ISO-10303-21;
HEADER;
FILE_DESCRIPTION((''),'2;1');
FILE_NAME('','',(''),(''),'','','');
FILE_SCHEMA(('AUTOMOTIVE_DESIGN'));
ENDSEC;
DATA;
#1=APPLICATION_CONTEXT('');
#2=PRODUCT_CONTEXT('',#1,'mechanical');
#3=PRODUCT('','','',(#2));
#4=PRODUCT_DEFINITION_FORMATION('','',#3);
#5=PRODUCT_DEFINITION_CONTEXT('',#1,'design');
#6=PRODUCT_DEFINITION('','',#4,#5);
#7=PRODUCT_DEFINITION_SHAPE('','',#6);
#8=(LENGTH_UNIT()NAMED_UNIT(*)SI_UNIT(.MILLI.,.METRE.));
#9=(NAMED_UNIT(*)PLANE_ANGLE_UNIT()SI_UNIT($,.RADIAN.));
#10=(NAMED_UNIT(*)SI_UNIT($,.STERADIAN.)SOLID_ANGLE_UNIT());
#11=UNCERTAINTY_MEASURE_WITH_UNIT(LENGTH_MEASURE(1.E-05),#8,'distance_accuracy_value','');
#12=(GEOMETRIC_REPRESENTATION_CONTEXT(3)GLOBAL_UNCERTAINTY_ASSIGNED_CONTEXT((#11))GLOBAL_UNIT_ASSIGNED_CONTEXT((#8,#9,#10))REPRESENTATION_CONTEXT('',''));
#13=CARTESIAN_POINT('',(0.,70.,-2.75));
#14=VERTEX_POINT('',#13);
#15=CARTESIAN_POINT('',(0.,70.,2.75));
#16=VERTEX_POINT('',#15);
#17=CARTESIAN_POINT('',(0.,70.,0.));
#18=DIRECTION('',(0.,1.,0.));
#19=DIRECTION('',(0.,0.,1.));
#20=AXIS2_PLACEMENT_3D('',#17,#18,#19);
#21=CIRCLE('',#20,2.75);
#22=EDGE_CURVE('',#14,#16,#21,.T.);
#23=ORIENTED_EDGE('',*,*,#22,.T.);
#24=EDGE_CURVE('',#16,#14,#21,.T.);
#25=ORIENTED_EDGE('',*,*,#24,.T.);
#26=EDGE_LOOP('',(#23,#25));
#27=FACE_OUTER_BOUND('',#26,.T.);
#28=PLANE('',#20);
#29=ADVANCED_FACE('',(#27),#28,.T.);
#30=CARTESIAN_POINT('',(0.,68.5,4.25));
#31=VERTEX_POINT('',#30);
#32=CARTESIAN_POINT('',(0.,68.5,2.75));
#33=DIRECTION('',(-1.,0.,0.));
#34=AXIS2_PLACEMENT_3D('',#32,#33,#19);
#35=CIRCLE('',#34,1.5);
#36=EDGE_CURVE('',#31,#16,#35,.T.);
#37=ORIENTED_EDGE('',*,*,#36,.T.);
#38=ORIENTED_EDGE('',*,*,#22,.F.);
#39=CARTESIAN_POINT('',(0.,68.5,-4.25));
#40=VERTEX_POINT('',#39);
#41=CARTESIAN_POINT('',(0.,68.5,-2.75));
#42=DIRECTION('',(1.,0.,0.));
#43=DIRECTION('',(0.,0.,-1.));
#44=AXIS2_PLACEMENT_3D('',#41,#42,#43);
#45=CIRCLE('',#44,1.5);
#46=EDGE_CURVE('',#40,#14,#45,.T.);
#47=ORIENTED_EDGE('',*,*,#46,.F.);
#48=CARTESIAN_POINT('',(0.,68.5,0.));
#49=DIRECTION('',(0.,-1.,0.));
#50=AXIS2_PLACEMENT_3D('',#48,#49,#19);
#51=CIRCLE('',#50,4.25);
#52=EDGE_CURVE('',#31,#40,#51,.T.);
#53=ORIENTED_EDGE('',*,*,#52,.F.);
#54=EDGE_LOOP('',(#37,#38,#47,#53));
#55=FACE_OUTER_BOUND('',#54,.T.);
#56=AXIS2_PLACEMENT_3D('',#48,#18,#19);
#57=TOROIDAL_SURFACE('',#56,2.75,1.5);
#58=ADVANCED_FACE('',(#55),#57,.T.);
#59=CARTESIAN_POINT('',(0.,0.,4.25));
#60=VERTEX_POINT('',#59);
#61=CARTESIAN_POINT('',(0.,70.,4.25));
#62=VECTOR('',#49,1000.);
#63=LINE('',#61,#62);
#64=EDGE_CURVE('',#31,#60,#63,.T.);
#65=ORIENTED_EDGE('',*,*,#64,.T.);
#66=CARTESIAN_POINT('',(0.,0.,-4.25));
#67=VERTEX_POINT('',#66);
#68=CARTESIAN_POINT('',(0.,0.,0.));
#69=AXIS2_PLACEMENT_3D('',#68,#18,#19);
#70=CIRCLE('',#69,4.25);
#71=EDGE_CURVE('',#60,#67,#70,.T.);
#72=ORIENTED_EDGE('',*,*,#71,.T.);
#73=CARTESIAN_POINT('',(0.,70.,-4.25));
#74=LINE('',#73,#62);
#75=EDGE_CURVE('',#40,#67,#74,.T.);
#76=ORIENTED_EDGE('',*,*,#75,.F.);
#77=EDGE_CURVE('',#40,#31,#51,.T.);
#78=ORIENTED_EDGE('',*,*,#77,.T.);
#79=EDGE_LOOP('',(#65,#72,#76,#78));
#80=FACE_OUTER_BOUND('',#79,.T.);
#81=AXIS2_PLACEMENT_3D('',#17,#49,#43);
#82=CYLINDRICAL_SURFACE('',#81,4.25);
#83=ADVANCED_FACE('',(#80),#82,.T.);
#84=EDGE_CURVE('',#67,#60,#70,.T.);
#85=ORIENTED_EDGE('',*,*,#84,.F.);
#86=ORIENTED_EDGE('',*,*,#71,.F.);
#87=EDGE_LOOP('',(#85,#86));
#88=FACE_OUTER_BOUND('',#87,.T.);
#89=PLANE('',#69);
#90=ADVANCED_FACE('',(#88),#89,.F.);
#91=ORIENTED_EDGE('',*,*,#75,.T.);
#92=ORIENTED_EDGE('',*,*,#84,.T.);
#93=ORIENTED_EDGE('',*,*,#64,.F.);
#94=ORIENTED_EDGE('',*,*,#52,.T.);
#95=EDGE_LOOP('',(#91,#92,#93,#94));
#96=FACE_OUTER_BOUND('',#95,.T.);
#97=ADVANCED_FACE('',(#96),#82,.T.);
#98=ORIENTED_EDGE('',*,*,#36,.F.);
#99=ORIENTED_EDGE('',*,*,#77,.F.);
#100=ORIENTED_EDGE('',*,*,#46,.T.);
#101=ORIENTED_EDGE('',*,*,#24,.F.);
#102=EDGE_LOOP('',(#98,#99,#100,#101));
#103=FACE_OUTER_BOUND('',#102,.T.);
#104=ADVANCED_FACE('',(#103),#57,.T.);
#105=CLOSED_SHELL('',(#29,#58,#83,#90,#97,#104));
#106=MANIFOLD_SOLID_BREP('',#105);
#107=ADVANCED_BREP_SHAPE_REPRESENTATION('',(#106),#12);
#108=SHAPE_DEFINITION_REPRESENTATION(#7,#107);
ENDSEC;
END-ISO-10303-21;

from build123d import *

# Parameters (mm, degrees)
SKETCH1_R           = 4.25
BOSS_EXTRUDE1_DEPTH = 70
FILLET1_R           = 1.5


with BuildPart() as part:
    # Sketch1 → Boss-Extrude1 (new body)
    with BuildSketch(Plane(origin=(0, 0, 0), x_dir=(1, 0, 0), z_dir=(0, 1, 0))):
        with Locations(Location((0, 0, 0), (0, 0, 270))):
            Circle(SKETCH1_R)
    extrude(amount=BOSS_EXTRUDE1_DEPTH)

    # Fillet1
    fillet1_edges = [part.edges().sort_by_distance(p)[0] for p in [
        (0, 70, -4.25),
    ]]
    fillet(fillet1_edges, radius=FILLET1_R)


solid = part.part
